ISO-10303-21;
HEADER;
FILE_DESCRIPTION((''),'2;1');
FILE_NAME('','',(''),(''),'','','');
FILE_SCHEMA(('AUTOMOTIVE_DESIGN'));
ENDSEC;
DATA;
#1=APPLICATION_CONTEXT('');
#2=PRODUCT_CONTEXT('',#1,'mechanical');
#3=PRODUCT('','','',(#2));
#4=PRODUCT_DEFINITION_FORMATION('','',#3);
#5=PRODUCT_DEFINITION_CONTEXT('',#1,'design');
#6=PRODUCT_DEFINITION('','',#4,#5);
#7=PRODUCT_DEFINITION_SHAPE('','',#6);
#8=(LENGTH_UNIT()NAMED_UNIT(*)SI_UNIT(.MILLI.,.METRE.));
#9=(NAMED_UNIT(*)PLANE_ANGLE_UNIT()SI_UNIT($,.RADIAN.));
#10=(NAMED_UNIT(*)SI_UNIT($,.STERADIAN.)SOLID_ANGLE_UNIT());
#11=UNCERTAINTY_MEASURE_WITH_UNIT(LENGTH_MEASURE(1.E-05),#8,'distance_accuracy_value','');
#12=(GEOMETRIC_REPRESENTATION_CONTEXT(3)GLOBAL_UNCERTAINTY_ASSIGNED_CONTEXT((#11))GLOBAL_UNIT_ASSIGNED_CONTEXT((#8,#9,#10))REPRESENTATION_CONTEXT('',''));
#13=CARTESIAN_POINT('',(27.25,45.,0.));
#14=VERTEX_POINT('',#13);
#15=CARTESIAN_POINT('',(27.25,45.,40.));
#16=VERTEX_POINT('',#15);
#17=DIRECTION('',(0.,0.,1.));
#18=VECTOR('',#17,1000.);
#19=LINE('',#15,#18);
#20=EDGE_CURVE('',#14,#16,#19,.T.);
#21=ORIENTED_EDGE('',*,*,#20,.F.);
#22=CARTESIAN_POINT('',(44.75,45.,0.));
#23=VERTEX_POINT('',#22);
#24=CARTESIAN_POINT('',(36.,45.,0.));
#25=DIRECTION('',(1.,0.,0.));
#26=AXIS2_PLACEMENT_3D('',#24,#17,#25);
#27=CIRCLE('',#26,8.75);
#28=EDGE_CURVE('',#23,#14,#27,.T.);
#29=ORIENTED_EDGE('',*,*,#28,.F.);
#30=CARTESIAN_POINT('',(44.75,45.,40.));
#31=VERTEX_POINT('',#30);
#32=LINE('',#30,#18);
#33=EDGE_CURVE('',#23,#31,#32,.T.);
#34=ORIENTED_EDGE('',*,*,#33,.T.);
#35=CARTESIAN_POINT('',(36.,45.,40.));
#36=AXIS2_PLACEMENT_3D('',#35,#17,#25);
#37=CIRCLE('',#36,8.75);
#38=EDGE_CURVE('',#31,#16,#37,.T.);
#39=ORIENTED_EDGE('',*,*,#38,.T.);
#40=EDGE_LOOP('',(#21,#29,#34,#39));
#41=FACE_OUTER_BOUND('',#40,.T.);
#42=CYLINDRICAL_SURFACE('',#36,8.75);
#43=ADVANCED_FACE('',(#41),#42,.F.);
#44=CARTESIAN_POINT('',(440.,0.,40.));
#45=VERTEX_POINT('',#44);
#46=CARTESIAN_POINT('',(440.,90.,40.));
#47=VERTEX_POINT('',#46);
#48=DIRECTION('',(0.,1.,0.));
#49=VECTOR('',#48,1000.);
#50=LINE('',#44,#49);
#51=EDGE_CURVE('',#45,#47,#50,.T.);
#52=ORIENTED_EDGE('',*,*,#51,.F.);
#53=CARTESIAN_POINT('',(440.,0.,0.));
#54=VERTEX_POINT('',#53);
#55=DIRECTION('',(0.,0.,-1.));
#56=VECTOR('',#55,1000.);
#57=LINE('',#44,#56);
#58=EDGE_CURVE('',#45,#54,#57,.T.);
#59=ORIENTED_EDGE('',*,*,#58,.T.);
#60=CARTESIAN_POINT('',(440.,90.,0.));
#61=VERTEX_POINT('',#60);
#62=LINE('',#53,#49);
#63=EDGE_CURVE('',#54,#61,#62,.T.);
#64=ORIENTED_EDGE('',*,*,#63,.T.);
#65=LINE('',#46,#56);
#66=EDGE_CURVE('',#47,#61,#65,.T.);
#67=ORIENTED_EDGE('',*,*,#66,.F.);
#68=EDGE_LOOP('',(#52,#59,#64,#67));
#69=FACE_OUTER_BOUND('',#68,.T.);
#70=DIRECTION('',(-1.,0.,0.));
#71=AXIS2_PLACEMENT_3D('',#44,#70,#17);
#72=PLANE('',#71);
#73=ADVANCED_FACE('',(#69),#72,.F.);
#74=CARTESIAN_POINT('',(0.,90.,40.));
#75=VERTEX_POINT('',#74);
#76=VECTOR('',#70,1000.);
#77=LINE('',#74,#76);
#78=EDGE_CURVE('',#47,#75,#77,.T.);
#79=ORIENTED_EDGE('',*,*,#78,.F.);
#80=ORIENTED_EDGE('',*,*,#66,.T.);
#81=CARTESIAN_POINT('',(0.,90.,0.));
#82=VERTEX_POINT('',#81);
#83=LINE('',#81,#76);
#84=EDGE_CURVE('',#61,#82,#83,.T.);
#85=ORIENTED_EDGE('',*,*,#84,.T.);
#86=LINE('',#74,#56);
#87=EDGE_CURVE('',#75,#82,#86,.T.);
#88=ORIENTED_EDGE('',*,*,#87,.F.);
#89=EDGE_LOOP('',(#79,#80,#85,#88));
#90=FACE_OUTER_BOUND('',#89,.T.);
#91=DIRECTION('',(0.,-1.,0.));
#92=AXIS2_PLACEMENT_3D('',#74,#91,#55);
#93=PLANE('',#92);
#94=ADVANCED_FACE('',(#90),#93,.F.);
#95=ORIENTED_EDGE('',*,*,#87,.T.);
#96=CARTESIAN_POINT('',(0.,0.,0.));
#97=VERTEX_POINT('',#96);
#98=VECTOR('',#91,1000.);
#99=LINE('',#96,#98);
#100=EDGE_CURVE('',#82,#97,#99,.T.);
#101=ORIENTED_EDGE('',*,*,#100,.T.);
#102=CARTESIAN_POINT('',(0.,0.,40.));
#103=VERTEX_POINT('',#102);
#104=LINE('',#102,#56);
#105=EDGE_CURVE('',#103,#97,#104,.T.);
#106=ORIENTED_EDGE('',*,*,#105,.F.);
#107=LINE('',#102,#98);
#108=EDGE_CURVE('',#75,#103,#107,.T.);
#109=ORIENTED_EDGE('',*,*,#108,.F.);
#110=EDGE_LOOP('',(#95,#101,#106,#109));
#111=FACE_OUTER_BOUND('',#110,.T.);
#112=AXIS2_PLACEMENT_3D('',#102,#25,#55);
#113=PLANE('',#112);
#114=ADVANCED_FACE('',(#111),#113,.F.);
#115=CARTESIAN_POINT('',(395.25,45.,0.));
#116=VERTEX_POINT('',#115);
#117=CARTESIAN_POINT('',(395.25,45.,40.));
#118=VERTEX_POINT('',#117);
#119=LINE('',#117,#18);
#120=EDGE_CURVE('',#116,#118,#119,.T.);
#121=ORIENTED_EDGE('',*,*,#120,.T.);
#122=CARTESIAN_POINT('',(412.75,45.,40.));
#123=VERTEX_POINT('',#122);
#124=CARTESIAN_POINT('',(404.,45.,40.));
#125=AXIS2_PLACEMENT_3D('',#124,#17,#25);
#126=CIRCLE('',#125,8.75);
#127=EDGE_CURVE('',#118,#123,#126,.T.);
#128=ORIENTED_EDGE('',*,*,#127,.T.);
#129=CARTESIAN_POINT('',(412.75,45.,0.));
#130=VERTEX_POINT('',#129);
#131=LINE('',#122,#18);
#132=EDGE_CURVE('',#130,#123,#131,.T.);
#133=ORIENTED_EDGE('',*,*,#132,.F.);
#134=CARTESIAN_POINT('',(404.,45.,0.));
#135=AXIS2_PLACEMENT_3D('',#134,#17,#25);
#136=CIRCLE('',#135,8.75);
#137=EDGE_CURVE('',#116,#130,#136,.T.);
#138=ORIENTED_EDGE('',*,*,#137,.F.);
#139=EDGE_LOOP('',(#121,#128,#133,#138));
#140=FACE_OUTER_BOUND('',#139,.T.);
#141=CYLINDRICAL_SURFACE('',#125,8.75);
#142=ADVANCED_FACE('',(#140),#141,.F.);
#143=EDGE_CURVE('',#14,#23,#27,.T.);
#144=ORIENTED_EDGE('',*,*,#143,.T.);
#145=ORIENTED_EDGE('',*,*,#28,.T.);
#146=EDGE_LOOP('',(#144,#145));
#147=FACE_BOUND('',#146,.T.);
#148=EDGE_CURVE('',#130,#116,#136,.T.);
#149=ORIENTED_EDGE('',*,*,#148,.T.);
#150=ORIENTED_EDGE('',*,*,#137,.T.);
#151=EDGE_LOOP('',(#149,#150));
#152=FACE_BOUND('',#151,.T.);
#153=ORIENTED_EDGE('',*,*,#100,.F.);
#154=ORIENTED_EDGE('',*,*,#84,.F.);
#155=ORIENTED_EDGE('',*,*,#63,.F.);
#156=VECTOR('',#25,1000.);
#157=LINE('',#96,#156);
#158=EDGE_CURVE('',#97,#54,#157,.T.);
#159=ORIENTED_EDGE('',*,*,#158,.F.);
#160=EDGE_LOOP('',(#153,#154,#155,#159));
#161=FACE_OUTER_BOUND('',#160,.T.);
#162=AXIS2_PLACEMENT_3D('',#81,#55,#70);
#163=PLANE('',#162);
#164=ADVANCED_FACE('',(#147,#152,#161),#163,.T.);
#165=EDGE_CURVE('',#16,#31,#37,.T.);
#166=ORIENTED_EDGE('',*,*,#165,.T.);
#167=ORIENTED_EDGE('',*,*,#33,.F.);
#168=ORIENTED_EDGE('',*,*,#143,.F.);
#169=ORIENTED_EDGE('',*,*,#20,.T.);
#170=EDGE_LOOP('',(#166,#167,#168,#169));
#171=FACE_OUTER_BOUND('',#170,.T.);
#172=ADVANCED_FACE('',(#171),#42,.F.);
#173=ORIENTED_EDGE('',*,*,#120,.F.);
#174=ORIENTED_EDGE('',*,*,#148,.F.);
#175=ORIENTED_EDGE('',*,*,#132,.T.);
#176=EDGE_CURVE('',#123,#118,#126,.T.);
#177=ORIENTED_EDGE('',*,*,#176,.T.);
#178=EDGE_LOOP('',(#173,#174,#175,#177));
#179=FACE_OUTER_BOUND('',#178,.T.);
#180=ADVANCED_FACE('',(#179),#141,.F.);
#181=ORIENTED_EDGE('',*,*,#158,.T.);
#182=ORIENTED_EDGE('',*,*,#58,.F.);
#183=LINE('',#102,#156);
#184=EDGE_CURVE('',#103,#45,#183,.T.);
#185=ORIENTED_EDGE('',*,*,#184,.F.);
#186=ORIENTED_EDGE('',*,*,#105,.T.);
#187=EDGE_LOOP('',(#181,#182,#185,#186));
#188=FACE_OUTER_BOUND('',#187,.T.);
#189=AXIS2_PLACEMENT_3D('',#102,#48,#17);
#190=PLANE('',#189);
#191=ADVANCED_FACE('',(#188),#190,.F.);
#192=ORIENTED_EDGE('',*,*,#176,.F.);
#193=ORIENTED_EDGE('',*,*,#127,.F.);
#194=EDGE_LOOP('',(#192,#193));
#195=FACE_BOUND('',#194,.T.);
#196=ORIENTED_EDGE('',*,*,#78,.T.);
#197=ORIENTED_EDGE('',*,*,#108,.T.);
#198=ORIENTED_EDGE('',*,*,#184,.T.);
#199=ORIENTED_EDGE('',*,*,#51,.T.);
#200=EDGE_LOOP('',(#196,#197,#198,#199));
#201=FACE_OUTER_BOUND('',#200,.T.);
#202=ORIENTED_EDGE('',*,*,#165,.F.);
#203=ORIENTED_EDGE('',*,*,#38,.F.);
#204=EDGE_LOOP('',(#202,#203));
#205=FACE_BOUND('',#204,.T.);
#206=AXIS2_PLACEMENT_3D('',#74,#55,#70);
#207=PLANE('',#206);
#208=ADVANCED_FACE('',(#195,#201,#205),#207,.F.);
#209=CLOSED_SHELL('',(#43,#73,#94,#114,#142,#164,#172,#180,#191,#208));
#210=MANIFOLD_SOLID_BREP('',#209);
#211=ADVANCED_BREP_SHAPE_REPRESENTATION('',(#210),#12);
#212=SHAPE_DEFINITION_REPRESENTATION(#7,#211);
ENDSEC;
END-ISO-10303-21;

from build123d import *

# Parameters (mm, degrees)
SKETCH1_W           = 440
SKETCH1_H           = 90
BOSS_EXTRUDE1_DEPTH = 40
M20_TAPPED_HOLE1_D  = 17.5


with BuildPart() as part:
    # Sketch1 → Boss-Extrude1 (new body)
    with BuildSketch(Plane.XY):
        with Locations((220, 45)):
            Rectangle(SKETCH1_W, SKETCH1_H)
    extrude(amount=BOSS_EXTRUDE1_DEPTH)

    # M20 Tapped Hole1 (through all)
    with Locations(Plane.XY.offset(40)):
        with Locations((36, 45), (404, 45)):
            Hole(M20_TAPPED_HOLE1_D / 2)


solid = part.part
